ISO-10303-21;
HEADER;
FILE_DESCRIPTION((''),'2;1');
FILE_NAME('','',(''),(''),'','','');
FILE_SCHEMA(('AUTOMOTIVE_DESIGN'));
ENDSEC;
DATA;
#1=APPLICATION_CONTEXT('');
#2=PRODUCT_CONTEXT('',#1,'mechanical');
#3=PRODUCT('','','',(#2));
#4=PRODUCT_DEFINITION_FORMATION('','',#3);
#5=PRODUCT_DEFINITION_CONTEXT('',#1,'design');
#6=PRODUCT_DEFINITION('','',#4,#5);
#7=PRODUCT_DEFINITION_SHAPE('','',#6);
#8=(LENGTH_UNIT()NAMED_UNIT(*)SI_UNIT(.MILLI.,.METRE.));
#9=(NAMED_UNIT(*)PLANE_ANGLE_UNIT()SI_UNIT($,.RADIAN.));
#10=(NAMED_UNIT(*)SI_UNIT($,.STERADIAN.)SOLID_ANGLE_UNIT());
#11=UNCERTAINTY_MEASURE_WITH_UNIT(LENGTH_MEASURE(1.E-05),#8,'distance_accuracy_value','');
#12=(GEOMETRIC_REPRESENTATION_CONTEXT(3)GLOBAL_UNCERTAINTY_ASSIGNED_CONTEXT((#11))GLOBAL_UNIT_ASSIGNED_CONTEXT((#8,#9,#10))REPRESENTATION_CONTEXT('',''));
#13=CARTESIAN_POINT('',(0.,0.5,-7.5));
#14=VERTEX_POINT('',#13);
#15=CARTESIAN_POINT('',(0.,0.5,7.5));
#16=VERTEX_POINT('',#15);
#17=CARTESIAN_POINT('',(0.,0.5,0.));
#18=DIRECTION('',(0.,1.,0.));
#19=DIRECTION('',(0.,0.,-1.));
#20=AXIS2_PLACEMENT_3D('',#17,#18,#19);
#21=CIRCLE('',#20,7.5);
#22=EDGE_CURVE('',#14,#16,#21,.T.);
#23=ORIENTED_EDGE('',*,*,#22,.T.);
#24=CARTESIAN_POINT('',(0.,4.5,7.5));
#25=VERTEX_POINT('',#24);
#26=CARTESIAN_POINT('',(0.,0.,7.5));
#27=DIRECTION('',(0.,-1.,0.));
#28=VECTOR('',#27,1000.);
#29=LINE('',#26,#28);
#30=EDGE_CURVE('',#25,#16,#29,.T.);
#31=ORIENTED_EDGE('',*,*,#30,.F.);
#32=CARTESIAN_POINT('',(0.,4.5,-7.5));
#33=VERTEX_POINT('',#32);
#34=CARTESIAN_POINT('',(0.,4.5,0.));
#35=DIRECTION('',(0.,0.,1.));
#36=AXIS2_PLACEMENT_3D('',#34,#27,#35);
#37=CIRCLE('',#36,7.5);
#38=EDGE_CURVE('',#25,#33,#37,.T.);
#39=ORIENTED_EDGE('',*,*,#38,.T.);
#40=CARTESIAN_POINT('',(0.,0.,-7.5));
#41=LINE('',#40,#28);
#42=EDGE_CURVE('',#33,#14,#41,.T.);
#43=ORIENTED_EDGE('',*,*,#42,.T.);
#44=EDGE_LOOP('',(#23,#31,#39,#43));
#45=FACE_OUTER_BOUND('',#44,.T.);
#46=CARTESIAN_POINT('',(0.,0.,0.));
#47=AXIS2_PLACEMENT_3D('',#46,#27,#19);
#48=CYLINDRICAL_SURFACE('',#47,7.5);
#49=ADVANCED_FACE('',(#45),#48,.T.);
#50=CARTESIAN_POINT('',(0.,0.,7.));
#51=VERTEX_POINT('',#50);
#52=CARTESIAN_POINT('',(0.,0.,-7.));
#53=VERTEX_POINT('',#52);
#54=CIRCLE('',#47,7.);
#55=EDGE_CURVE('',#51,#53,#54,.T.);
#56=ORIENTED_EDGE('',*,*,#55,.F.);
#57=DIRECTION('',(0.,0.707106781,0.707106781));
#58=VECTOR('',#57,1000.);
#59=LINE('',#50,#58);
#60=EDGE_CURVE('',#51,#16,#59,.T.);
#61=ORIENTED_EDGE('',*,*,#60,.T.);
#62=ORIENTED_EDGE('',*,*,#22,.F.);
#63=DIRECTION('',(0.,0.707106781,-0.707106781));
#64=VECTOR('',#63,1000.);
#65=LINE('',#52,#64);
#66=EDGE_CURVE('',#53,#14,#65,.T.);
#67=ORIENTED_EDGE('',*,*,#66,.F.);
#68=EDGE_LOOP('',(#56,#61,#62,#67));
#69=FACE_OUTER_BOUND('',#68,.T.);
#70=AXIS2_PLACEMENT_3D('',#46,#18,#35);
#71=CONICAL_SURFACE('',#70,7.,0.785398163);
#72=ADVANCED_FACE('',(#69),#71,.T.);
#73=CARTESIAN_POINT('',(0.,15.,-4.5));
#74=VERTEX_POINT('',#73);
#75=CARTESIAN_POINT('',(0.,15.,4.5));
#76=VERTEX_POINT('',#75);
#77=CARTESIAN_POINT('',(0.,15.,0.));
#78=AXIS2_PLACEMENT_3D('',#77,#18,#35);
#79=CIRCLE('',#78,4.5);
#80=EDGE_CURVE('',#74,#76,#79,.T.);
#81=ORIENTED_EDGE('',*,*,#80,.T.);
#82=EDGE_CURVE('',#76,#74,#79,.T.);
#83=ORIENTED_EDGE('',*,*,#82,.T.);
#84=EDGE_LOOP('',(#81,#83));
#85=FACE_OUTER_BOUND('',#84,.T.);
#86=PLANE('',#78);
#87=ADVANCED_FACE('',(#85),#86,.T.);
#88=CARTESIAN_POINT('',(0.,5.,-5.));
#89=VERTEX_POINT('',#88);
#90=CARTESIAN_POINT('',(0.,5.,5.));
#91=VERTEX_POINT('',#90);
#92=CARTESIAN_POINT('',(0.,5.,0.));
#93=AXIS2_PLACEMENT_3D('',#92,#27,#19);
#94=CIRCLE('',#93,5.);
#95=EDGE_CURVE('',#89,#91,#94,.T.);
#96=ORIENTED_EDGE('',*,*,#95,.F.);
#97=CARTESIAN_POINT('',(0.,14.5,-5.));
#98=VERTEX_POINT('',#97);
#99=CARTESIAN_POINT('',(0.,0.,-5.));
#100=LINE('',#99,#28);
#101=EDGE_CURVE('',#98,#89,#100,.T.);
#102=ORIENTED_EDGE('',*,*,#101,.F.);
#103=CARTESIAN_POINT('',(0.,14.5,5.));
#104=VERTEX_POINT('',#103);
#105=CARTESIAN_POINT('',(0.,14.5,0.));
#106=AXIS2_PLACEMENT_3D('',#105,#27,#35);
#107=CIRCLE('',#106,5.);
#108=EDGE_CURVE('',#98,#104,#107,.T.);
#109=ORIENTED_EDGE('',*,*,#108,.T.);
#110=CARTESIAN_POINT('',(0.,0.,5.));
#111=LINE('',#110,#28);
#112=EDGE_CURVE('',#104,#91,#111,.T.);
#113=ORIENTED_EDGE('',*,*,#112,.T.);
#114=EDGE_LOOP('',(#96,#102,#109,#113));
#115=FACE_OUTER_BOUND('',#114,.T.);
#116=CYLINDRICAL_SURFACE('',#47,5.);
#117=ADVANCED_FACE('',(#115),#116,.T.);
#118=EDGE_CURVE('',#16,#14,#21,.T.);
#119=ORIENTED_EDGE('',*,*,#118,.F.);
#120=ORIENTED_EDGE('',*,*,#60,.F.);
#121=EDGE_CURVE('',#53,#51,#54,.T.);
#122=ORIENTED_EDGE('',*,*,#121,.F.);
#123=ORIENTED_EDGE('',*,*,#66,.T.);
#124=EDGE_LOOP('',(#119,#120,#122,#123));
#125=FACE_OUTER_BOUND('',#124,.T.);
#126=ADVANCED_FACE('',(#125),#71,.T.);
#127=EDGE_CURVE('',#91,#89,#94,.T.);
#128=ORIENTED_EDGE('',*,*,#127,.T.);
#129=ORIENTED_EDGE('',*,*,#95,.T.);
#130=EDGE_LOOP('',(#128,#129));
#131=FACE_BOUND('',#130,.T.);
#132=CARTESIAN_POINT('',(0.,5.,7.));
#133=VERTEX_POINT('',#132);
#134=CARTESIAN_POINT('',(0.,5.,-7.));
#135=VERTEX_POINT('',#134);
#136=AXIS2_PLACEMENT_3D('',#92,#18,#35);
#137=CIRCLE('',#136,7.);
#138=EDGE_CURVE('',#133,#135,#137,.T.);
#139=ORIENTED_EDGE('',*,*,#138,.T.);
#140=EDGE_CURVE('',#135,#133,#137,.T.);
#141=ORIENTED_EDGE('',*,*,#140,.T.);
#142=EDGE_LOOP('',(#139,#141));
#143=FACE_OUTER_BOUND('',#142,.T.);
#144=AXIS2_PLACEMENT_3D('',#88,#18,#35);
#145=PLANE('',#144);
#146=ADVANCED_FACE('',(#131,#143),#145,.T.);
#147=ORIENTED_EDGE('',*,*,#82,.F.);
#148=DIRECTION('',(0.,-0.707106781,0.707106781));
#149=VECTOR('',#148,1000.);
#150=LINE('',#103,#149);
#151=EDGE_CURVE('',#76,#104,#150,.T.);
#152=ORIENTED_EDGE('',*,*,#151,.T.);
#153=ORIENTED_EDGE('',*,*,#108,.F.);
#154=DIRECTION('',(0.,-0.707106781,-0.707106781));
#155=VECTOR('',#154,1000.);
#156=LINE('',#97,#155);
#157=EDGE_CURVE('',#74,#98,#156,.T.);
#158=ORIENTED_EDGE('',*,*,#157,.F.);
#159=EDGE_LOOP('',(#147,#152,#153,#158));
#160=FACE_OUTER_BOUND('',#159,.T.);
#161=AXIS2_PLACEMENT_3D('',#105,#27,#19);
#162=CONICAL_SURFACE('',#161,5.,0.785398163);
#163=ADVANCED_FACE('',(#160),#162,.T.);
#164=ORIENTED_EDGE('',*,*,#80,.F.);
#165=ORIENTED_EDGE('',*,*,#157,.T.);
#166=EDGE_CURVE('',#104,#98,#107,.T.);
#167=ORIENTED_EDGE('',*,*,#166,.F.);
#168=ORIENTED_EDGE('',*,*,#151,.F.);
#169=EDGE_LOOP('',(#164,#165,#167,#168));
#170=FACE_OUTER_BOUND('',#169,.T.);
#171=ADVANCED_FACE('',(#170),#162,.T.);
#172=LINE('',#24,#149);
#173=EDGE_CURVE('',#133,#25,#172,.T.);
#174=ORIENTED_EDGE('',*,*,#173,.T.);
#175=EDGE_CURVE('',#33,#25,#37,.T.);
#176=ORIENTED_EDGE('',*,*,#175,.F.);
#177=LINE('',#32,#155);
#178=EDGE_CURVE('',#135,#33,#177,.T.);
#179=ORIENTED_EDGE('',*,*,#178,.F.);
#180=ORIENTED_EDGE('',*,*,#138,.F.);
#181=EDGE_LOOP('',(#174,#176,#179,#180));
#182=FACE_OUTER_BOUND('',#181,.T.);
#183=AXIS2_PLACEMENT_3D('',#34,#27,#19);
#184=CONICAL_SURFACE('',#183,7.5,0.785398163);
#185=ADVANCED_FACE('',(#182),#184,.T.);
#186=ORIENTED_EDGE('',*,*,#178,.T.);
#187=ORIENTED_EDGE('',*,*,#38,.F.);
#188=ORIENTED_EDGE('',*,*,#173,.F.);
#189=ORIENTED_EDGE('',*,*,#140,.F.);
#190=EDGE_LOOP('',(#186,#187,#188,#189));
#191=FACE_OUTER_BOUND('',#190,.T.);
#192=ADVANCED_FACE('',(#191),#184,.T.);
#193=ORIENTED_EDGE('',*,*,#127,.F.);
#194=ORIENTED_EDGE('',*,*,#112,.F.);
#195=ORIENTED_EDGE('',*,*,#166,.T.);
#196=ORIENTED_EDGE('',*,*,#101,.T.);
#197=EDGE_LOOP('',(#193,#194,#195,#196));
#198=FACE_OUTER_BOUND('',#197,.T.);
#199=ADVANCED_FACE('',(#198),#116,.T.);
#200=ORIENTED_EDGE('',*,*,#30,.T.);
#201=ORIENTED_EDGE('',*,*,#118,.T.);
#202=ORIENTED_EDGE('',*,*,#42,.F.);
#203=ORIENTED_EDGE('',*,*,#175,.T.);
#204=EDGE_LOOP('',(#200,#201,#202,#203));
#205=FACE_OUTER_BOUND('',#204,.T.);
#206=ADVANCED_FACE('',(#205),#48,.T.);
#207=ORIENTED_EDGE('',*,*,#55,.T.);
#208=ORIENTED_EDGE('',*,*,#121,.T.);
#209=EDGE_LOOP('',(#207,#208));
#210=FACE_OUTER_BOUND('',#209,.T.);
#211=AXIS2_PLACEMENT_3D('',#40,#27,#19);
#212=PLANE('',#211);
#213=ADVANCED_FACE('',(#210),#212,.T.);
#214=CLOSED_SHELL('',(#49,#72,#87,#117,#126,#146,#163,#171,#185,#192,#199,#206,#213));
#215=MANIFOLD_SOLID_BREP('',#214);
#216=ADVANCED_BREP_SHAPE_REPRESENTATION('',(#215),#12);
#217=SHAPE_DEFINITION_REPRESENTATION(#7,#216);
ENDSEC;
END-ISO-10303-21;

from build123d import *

# Parameters (mm, degrees)
CHAMFER1_SIZE = 0.5


with BuildPart() as part:
    # Sketch1 → Revolve1 (revolve)
    with BuildSketch(Plane(origin=(0, 0, 0), x_dir=(0, 0, -1), z_dir=(1, 0, 0))):
        Polygon((0, 15), (5, 15), (5, 5), (7.5, 5), (7.5, 0), (0, 0), align=None)
    revolve(axis=Axis((0, 0, 0), (0, 1, 0)))

    # Chamfer1
    chamfer1_edges = [part.edges().sort_by_distance(p)[0] for p in [
        (0, 0, 7.5),
        (0, 5, 7.5),
        (0, 15, 5),
    ]]
    chamfer(chamfer1_edges, length=CHAMFER1_SIZE)


solid = part.part
